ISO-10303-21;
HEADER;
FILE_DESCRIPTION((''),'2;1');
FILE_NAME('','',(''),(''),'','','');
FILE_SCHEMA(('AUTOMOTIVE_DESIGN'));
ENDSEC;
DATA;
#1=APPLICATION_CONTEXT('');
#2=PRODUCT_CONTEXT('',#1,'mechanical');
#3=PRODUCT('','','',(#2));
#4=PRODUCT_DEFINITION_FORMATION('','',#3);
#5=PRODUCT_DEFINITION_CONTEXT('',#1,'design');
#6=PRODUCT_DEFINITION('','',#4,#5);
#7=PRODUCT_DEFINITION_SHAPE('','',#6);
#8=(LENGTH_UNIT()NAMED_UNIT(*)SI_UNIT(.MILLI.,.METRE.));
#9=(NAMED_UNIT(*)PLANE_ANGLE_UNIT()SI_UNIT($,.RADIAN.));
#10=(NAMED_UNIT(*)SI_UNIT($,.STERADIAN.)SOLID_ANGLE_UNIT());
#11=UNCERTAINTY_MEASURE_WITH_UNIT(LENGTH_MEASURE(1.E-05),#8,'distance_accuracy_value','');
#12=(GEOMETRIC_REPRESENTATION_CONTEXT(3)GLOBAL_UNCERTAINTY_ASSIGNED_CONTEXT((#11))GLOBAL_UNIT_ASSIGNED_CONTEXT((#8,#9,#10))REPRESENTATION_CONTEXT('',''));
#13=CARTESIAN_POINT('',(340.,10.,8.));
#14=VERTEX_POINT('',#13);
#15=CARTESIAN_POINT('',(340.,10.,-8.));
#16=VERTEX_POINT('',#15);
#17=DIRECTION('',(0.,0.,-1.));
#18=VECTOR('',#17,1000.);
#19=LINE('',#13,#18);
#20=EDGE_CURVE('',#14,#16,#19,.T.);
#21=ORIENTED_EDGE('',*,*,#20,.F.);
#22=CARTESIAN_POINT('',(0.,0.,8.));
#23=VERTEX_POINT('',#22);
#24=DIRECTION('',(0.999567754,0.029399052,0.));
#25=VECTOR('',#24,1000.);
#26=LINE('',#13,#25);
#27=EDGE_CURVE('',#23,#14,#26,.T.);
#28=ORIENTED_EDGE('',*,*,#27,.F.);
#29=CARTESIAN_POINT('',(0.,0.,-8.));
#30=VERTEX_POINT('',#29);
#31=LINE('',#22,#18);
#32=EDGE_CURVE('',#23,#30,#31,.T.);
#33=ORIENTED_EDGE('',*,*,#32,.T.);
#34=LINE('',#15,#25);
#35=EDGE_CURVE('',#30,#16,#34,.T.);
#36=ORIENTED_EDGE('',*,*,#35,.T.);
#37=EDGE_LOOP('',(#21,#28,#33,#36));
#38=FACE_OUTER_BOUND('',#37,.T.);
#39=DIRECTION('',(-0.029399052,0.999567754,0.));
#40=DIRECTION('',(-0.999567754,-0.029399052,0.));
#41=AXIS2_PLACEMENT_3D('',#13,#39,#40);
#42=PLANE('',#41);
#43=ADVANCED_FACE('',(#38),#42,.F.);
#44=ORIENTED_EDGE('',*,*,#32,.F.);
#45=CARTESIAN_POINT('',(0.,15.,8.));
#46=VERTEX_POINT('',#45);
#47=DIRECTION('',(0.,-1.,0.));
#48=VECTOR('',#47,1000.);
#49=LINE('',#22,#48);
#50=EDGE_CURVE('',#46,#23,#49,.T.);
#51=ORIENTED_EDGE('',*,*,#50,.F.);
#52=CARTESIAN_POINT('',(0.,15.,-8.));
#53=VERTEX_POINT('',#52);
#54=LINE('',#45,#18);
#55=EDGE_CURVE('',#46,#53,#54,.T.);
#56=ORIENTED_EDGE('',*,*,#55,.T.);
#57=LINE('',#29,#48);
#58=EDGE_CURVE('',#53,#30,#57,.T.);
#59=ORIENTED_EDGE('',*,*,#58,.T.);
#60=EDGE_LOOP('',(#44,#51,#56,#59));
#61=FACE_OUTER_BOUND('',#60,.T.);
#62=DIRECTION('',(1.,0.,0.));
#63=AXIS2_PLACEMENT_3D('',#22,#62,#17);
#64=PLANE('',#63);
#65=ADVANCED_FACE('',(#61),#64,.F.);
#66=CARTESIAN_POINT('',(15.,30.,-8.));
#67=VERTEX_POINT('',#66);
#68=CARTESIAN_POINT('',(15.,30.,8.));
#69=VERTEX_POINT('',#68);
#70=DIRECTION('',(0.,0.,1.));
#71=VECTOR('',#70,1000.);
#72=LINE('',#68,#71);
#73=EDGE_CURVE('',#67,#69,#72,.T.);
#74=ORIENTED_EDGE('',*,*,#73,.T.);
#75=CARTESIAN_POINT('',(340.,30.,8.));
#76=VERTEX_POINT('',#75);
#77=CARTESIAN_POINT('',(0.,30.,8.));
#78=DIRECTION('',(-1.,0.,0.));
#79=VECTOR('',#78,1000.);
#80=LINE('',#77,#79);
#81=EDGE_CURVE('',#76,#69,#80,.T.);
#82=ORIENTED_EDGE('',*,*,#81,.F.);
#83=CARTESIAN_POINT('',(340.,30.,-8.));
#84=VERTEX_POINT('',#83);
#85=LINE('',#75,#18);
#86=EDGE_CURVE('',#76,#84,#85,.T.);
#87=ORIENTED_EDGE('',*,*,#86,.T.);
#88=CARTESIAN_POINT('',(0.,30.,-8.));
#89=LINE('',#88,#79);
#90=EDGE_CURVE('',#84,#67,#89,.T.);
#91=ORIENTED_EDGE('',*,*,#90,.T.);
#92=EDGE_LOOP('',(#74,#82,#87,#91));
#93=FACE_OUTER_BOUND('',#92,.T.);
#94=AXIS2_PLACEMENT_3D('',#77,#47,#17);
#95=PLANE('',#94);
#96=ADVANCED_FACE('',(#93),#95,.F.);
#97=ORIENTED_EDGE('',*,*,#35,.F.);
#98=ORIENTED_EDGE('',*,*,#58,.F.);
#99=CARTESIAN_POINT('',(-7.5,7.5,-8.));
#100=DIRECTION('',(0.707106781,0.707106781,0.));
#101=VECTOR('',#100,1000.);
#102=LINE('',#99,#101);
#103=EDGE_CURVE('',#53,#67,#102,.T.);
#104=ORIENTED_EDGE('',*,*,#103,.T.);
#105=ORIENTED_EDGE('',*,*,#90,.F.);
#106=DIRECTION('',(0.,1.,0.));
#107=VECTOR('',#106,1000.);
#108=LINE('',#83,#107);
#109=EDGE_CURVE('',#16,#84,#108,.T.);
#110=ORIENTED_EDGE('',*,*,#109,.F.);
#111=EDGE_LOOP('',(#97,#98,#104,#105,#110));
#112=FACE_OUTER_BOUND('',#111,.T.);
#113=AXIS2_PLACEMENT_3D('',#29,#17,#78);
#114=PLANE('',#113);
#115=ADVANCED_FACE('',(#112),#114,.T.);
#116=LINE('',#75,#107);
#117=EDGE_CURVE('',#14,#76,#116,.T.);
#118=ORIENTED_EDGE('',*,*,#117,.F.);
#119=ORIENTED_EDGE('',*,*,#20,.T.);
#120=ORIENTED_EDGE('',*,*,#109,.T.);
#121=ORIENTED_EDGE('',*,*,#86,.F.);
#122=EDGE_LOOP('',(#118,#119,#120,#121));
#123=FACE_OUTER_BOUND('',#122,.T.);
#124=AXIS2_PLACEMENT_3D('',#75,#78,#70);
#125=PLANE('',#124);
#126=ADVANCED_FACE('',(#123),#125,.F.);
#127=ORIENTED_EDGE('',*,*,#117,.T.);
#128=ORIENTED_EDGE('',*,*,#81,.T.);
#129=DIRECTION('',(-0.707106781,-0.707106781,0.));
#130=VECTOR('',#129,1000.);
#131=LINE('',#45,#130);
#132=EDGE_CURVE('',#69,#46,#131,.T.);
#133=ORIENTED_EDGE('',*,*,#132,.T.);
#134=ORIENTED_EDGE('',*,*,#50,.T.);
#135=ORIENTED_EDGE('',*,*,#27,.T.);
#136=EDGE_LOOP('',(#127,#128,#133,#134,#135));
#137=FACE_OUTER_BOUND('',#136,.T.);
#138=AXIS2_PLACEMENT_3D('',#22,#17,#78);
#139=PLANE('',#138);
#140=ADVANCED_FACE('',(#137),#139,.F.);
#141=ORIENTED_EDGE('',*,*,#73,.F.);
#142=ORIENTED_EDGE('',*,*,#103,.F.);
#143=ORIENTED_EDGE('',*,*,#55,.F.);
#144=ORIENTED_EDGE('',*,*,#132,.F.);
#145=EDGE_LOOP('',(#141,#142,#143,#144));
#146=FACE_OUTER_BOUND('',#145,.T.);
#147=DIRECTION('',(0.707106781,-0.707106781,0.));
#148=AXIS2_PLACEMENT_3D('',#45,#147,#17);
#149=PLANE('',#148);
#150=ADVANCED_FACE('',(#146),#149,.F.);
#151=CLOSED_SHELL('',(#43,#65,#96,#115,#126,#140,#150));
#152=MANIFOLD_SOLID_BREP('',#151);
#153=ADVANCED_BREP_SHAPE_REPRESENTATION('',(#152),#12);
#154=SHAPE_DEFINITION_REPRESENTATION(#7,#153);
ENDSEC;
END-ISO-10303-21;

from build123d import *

# Parameters (mm, degrees)
BOSS_EXTRUDE1_DEPTH = 8
CHAMFER1_SIZE       = 15


with BuildPart() as part:
    # Sketch1 → Boss-Extrude1 (new, symmetric)
    with BuildSketch(Plane.XY):
        Polygon((0, 0), (0, 30), (340, 30), (340, 10), align=None)
    extrude(amount=BOSS_EXTRUDE1_DEPTH, both=True)

    # Chamfer1
    chamfer1_edges = [part.edges().sort_by_distance(p)[0] for p in [
        (0, 30, 0),
    ]]
    chamfer(chamfer1_edges, length=CHAMFER1_SIZE)


solid = part.part
